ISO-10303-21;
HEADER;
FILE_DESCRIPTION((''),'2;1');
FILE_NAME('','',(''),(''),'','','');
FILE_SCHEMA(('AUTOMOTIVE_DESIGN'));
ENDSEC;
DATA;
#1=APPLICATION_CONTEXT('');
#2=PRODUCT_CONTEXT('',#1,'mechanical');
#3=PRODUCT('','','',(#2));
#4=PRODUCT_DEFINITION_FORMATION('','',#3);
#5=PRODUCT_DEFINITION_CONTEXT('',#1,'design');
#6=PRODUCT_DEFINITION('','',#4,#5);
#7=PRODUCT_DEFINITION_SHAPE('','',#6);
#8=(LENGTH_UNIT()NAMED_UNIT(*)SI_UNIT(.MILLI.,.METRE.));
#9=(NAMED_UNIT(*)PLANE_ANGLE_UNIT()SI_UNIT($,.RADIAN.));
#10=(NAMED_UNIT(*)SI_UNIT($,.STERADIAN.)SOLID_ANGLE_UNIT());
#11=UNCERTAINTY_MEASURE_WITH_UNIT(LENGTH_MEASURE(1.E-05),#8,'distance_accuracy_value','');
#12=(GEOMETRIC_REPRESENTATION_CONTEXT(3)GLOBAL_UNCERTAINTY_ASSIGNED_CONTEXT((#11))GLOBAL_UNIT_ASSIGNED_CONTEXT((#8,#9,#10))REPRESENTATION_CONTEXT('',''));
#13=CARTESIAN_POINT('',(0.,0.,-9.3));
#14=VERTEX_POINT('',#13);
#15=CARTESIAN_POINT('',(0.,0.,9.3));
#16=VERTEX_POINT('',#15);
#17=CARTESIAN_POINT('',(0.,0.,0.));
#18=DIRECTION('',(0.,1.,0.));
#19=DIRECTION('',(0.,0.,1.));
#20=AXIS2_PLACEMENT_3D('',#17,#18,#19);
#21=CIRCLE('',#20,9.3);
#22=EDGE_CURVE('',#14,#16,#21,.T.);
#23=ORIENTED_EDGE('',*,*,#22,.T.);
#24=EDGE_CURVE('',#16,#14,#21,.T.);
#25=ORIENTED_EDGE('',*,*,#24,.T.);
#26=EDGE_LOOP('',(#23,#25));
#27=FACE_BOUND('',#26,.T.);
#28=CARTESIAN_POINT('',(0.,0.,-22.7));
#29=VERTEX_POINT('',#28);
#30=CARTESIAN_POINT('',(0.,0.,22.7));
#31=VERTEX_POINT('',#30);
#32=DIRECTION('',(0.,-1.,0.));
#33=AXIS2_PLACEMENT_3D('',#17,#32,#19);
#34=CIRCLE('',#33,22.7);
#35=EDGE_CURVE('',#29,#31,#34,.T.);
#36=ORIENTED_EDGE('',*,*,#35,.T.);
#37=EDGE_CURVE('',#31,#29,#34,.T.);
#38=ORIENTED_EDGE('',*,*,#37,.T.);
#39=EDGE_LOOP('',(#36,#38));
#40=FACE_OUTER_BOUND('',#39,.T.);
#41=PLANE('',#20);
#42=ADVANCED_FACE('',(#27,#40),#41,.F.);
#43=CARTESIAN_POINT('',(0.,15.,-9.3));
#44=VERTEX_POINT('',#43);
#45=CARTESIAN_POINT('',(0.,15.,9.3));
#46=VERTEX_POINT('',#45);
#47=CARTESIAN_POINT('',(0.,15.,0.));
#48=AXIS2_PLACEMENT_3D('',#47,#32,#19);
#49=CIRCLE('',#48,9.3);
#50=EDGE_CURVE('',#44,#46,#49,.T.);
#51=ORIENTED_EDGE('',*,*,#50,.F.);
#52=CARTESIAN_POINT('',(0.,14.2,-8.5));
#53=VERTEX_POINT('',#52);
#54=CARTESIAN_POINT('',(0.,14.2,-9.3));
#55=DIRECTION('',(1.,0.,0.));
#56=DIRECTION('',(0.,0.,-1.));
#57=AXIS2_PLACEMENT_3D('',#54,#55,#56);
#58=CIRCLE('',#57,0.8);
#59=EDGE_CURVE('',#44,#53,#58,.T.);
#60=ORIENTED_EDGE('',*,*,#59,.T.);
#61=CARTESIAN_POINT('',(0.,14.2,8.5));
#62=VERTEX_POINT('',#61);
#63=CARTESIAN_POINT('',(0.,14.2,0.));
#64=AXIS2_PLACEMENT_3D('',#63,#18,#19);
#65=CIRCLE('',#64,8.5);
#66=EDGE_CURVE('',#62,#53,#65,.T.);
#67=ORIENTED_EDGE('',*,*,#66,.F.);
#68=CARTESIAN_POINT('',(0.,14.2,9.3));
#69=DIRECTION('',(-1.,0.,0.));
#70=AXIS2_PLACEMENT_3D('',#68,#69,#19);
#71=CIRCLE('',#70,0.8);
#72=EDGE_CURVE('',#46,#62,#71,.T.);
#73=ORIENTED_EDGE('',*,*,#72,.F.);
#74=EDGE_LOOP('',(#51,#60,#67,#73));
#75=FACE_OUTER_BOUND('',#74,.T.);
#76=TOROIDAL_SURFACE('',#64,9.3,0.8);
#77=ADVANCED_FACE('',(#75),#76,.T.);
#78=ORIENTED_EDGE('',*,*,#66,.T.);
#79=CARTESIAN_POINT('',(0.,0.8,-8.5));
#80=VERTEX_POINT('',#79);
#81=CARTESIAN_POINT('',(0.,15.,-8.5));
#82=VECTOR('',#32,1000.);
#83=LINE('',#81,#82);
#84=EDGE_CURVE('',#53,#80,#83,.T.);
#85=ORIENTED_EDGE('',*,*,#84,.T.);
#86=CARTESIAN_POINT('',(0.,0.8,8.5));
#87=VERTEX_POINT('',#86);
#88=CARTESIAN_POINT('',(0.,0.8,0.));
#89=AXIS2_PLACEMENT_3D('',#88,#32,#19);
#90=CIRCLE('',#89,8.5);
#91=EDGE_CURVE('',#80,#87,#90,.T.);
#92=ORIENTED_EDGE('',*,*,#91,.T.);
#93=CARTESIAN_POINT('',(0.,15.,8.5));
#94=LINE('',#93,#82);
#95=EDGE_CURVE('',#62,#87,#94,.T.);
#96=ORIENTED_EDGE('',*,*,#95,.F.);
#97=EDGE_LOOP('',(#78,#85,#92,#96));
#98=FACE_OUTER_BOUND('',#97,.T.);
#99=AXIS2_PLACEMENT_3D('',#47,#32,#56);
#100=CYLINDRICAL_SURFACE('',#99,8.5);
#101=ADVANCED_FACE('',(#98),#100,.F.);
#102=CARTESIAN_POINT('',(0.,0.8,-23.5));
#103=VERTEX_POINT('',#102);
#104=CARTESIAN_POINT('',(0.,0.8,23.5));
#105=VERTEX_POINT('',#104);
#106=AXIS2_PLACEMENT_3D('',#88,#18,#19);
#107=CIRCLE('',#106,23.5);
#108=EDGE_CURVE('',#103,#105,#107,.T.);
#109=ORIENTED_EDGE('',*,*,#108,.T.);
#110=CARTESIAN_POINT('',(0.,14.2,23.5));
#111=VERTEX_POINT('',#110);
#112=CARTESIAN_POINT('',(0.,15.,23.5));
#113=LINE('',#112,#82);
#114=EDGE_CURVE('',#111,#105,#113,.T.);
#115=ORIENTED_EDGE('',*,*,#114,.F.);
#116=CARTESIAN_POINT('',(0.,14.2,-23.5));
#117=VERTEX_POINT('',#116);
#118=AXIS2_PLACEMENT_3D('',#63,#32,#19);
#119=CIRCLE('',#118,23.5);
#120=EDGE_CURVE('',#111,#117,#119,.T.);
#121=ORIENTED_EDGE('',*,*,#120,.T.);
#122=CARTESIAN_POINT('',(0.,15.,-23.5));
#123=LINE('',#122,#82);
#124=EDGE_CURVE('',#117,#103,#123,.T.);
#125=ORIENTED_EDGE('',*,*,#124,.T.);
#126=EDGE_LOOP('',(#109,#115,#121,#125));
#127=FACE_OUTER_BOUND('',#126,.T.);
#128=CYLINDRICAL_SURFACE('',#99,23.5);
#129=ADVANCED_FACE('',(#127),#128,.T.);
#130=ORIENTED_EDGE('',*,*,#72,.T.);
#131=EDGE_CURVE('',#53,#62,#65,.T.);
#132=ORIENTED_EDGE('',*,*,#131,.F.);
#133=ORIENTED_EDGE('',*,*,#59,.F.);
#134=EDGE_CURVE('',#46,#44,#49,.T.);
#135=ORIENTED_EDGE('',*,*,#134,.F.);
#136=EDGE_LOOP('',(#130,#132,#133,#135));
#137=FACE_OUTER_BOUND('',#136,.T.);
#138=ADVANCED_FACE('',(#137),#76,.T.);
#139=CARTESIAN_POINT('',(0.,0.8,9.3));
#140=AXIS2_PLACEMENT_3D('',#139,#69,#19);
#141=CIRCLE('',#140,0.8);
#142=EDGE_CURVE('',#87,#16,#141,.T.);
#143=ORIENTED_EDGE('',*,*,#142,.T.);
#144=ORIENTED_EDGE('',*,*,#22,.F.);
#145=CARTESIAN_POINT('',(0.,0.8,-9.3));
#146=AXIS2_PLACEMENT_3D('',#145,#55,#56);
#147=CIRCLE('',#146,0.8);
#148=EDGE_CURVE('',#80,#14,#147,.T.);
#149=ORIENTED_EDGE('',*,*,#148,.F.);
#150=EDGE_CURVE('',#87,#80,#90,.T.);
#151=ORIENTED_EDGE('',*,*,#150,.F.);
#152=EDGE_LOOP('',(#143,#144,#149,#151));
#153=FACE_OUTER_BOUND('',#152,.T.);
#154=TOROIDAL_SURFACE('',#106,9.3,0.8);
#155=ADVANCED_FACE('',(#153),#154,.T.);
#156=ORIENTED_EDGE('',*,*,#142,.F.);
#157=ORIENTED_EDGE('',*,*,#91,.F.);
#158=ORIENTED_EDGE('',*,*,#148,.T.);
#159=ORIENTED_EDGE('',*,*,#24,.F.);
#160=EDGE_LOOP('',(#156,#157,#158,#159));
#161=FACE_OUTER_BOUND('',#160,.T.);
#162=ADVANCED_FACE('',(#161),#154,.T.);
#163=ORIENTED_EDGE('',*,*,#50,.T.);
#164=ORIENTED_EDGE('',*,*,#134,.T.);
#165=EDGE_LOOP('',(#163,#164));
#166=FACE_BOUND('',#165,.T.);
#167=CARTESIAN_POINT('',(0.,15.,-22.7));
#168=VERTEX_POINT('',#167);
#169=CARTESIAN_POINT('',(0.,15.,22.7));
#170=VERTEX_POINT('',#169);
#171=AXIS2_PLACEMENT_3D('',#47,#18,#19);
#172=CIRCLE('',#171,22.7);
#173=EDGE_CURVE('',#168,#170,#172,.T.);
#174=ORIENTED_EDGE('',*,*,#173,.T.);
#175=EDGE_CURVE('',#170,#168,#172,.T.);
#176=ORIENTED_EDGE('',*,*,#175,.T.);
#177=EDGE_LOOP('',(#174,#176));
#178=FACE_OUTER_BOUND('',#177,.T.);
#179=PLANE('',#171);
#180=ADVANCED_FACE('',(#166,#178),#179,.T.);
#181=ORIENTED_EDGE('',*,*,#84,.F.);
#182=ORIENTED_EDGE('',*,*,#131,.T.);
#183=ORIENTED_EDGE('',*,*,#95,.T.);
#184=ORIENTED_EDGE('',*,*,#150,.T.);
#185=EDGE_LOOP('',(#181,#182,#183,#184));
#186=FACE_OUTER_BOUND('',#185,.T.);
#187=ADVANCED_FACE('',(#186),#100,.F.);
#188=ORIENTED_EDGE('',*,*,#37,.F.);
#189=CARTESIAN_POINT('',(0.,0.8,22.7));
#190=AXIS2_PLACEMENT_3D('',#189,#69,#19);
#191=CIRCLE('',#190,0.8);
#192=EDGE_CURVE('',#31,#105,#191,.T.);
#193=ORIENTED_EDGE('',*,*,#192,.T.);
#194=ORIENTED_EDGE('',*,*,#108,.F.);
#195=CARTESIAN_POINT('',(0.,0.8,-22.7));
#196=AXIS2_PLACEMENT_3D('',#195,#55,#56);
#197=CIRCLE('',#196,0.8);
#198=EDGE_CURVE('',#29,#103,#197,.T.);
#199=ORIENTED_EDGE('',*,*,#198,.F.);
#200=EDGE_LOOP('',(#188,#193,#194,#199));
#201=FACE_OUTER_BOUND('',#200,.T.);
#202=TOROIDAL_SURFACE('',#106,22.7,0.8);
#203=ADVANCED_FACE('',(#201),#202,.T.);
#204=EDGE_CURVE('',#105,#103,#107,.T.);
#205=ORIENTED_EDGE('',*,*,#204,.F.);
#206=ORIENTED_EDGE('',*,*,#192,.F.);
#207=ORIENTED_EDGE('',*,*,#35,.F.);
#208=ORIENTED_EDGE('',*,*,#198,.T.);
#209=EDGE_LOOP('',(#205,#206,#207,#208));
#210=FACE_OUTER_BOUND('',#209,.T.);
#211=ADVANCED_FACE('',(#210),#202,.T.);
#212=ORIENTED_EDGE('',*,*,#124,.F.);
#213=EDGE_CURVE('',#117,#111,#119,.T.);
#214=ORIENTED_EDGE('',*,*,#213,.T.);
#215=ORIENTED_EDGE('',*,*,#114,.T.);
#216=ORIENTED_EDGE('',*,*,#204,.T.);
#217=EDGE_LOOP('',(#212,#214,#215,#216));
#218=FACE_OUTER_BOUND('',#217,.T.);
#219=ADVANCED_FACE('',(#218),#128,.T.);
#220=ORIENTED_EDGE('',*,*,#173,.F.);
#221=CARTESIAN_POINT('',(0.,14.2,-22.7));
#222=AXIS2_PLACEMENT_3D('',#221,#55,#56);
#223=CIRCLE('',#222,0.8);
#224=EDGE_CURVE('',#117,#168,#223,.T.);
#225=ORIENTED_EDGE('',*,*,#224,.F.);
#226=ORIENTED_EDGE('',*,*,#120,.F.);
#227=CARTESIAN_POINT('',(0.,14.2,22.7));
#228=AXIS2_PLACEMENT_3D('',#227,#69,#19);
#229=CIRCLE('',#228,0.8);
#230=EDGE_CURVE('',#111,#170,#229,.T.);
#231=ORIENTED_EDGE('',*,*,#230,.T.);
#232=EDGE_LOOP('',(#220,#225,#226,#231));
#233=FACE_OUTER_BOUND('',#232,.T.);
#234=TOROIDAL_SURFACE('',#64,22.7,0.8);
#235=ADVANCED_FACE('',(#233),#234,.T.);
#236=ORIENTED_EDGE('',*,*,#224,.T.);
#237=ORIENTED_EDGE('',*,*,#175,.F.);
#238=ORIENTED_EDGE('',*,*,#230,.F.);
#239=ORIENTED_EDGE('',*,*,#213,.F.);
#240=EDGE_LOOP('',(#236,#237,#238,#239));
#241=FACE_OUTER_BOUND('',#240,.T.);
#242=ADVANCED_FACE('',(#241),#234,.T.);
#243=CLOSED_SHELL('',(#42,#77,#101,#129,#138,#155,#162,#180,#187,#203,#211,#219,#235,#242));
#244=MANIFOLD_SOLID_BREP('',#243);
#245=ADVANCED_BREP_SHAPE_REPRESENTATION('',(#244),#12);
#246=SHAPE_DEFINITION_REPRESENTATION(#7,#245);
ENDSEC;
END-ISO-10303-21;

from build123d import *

# Parameters (mm, degrees)
SKETCH_1_R      = 23.5
SKETCH_1_R_2    = 8.5
EXTRUDE_1_DEPTH = 15
FILLET_1_R      = 0.8


with BuildPart() as part:
    # 草图1 → 拉伸1 (new body)
    with BuildSketch(Plane(origin=(0, 0, 0), x_dir=(1, 0, 0), z_dir=(0, 1, 0))):
        with Locations(Location((0, 0, 0), (0, 0, 270))):
            Circle(SKETCH_1_R)
        with Locations(Location((0, 0, 0), (0, 0, 270))):
            Circle(SKETCH_1_R_2, mode=Mode.SUBTRACT)
    extrude(amount=EXTRUDE_1_DEPTH)

    # 圆角1
    fillet_1_edges = [part.edges().sort_by_distance(p)[0] for p in [
        (0, 0, -23.5),
        (0, 15, -23.5),
        (0, 0, -8.5),
        (0, 15, -8.5),
    ]]
    fillet(fillet_1_edges, radius=FILLET_1_R)


solid = part.part
